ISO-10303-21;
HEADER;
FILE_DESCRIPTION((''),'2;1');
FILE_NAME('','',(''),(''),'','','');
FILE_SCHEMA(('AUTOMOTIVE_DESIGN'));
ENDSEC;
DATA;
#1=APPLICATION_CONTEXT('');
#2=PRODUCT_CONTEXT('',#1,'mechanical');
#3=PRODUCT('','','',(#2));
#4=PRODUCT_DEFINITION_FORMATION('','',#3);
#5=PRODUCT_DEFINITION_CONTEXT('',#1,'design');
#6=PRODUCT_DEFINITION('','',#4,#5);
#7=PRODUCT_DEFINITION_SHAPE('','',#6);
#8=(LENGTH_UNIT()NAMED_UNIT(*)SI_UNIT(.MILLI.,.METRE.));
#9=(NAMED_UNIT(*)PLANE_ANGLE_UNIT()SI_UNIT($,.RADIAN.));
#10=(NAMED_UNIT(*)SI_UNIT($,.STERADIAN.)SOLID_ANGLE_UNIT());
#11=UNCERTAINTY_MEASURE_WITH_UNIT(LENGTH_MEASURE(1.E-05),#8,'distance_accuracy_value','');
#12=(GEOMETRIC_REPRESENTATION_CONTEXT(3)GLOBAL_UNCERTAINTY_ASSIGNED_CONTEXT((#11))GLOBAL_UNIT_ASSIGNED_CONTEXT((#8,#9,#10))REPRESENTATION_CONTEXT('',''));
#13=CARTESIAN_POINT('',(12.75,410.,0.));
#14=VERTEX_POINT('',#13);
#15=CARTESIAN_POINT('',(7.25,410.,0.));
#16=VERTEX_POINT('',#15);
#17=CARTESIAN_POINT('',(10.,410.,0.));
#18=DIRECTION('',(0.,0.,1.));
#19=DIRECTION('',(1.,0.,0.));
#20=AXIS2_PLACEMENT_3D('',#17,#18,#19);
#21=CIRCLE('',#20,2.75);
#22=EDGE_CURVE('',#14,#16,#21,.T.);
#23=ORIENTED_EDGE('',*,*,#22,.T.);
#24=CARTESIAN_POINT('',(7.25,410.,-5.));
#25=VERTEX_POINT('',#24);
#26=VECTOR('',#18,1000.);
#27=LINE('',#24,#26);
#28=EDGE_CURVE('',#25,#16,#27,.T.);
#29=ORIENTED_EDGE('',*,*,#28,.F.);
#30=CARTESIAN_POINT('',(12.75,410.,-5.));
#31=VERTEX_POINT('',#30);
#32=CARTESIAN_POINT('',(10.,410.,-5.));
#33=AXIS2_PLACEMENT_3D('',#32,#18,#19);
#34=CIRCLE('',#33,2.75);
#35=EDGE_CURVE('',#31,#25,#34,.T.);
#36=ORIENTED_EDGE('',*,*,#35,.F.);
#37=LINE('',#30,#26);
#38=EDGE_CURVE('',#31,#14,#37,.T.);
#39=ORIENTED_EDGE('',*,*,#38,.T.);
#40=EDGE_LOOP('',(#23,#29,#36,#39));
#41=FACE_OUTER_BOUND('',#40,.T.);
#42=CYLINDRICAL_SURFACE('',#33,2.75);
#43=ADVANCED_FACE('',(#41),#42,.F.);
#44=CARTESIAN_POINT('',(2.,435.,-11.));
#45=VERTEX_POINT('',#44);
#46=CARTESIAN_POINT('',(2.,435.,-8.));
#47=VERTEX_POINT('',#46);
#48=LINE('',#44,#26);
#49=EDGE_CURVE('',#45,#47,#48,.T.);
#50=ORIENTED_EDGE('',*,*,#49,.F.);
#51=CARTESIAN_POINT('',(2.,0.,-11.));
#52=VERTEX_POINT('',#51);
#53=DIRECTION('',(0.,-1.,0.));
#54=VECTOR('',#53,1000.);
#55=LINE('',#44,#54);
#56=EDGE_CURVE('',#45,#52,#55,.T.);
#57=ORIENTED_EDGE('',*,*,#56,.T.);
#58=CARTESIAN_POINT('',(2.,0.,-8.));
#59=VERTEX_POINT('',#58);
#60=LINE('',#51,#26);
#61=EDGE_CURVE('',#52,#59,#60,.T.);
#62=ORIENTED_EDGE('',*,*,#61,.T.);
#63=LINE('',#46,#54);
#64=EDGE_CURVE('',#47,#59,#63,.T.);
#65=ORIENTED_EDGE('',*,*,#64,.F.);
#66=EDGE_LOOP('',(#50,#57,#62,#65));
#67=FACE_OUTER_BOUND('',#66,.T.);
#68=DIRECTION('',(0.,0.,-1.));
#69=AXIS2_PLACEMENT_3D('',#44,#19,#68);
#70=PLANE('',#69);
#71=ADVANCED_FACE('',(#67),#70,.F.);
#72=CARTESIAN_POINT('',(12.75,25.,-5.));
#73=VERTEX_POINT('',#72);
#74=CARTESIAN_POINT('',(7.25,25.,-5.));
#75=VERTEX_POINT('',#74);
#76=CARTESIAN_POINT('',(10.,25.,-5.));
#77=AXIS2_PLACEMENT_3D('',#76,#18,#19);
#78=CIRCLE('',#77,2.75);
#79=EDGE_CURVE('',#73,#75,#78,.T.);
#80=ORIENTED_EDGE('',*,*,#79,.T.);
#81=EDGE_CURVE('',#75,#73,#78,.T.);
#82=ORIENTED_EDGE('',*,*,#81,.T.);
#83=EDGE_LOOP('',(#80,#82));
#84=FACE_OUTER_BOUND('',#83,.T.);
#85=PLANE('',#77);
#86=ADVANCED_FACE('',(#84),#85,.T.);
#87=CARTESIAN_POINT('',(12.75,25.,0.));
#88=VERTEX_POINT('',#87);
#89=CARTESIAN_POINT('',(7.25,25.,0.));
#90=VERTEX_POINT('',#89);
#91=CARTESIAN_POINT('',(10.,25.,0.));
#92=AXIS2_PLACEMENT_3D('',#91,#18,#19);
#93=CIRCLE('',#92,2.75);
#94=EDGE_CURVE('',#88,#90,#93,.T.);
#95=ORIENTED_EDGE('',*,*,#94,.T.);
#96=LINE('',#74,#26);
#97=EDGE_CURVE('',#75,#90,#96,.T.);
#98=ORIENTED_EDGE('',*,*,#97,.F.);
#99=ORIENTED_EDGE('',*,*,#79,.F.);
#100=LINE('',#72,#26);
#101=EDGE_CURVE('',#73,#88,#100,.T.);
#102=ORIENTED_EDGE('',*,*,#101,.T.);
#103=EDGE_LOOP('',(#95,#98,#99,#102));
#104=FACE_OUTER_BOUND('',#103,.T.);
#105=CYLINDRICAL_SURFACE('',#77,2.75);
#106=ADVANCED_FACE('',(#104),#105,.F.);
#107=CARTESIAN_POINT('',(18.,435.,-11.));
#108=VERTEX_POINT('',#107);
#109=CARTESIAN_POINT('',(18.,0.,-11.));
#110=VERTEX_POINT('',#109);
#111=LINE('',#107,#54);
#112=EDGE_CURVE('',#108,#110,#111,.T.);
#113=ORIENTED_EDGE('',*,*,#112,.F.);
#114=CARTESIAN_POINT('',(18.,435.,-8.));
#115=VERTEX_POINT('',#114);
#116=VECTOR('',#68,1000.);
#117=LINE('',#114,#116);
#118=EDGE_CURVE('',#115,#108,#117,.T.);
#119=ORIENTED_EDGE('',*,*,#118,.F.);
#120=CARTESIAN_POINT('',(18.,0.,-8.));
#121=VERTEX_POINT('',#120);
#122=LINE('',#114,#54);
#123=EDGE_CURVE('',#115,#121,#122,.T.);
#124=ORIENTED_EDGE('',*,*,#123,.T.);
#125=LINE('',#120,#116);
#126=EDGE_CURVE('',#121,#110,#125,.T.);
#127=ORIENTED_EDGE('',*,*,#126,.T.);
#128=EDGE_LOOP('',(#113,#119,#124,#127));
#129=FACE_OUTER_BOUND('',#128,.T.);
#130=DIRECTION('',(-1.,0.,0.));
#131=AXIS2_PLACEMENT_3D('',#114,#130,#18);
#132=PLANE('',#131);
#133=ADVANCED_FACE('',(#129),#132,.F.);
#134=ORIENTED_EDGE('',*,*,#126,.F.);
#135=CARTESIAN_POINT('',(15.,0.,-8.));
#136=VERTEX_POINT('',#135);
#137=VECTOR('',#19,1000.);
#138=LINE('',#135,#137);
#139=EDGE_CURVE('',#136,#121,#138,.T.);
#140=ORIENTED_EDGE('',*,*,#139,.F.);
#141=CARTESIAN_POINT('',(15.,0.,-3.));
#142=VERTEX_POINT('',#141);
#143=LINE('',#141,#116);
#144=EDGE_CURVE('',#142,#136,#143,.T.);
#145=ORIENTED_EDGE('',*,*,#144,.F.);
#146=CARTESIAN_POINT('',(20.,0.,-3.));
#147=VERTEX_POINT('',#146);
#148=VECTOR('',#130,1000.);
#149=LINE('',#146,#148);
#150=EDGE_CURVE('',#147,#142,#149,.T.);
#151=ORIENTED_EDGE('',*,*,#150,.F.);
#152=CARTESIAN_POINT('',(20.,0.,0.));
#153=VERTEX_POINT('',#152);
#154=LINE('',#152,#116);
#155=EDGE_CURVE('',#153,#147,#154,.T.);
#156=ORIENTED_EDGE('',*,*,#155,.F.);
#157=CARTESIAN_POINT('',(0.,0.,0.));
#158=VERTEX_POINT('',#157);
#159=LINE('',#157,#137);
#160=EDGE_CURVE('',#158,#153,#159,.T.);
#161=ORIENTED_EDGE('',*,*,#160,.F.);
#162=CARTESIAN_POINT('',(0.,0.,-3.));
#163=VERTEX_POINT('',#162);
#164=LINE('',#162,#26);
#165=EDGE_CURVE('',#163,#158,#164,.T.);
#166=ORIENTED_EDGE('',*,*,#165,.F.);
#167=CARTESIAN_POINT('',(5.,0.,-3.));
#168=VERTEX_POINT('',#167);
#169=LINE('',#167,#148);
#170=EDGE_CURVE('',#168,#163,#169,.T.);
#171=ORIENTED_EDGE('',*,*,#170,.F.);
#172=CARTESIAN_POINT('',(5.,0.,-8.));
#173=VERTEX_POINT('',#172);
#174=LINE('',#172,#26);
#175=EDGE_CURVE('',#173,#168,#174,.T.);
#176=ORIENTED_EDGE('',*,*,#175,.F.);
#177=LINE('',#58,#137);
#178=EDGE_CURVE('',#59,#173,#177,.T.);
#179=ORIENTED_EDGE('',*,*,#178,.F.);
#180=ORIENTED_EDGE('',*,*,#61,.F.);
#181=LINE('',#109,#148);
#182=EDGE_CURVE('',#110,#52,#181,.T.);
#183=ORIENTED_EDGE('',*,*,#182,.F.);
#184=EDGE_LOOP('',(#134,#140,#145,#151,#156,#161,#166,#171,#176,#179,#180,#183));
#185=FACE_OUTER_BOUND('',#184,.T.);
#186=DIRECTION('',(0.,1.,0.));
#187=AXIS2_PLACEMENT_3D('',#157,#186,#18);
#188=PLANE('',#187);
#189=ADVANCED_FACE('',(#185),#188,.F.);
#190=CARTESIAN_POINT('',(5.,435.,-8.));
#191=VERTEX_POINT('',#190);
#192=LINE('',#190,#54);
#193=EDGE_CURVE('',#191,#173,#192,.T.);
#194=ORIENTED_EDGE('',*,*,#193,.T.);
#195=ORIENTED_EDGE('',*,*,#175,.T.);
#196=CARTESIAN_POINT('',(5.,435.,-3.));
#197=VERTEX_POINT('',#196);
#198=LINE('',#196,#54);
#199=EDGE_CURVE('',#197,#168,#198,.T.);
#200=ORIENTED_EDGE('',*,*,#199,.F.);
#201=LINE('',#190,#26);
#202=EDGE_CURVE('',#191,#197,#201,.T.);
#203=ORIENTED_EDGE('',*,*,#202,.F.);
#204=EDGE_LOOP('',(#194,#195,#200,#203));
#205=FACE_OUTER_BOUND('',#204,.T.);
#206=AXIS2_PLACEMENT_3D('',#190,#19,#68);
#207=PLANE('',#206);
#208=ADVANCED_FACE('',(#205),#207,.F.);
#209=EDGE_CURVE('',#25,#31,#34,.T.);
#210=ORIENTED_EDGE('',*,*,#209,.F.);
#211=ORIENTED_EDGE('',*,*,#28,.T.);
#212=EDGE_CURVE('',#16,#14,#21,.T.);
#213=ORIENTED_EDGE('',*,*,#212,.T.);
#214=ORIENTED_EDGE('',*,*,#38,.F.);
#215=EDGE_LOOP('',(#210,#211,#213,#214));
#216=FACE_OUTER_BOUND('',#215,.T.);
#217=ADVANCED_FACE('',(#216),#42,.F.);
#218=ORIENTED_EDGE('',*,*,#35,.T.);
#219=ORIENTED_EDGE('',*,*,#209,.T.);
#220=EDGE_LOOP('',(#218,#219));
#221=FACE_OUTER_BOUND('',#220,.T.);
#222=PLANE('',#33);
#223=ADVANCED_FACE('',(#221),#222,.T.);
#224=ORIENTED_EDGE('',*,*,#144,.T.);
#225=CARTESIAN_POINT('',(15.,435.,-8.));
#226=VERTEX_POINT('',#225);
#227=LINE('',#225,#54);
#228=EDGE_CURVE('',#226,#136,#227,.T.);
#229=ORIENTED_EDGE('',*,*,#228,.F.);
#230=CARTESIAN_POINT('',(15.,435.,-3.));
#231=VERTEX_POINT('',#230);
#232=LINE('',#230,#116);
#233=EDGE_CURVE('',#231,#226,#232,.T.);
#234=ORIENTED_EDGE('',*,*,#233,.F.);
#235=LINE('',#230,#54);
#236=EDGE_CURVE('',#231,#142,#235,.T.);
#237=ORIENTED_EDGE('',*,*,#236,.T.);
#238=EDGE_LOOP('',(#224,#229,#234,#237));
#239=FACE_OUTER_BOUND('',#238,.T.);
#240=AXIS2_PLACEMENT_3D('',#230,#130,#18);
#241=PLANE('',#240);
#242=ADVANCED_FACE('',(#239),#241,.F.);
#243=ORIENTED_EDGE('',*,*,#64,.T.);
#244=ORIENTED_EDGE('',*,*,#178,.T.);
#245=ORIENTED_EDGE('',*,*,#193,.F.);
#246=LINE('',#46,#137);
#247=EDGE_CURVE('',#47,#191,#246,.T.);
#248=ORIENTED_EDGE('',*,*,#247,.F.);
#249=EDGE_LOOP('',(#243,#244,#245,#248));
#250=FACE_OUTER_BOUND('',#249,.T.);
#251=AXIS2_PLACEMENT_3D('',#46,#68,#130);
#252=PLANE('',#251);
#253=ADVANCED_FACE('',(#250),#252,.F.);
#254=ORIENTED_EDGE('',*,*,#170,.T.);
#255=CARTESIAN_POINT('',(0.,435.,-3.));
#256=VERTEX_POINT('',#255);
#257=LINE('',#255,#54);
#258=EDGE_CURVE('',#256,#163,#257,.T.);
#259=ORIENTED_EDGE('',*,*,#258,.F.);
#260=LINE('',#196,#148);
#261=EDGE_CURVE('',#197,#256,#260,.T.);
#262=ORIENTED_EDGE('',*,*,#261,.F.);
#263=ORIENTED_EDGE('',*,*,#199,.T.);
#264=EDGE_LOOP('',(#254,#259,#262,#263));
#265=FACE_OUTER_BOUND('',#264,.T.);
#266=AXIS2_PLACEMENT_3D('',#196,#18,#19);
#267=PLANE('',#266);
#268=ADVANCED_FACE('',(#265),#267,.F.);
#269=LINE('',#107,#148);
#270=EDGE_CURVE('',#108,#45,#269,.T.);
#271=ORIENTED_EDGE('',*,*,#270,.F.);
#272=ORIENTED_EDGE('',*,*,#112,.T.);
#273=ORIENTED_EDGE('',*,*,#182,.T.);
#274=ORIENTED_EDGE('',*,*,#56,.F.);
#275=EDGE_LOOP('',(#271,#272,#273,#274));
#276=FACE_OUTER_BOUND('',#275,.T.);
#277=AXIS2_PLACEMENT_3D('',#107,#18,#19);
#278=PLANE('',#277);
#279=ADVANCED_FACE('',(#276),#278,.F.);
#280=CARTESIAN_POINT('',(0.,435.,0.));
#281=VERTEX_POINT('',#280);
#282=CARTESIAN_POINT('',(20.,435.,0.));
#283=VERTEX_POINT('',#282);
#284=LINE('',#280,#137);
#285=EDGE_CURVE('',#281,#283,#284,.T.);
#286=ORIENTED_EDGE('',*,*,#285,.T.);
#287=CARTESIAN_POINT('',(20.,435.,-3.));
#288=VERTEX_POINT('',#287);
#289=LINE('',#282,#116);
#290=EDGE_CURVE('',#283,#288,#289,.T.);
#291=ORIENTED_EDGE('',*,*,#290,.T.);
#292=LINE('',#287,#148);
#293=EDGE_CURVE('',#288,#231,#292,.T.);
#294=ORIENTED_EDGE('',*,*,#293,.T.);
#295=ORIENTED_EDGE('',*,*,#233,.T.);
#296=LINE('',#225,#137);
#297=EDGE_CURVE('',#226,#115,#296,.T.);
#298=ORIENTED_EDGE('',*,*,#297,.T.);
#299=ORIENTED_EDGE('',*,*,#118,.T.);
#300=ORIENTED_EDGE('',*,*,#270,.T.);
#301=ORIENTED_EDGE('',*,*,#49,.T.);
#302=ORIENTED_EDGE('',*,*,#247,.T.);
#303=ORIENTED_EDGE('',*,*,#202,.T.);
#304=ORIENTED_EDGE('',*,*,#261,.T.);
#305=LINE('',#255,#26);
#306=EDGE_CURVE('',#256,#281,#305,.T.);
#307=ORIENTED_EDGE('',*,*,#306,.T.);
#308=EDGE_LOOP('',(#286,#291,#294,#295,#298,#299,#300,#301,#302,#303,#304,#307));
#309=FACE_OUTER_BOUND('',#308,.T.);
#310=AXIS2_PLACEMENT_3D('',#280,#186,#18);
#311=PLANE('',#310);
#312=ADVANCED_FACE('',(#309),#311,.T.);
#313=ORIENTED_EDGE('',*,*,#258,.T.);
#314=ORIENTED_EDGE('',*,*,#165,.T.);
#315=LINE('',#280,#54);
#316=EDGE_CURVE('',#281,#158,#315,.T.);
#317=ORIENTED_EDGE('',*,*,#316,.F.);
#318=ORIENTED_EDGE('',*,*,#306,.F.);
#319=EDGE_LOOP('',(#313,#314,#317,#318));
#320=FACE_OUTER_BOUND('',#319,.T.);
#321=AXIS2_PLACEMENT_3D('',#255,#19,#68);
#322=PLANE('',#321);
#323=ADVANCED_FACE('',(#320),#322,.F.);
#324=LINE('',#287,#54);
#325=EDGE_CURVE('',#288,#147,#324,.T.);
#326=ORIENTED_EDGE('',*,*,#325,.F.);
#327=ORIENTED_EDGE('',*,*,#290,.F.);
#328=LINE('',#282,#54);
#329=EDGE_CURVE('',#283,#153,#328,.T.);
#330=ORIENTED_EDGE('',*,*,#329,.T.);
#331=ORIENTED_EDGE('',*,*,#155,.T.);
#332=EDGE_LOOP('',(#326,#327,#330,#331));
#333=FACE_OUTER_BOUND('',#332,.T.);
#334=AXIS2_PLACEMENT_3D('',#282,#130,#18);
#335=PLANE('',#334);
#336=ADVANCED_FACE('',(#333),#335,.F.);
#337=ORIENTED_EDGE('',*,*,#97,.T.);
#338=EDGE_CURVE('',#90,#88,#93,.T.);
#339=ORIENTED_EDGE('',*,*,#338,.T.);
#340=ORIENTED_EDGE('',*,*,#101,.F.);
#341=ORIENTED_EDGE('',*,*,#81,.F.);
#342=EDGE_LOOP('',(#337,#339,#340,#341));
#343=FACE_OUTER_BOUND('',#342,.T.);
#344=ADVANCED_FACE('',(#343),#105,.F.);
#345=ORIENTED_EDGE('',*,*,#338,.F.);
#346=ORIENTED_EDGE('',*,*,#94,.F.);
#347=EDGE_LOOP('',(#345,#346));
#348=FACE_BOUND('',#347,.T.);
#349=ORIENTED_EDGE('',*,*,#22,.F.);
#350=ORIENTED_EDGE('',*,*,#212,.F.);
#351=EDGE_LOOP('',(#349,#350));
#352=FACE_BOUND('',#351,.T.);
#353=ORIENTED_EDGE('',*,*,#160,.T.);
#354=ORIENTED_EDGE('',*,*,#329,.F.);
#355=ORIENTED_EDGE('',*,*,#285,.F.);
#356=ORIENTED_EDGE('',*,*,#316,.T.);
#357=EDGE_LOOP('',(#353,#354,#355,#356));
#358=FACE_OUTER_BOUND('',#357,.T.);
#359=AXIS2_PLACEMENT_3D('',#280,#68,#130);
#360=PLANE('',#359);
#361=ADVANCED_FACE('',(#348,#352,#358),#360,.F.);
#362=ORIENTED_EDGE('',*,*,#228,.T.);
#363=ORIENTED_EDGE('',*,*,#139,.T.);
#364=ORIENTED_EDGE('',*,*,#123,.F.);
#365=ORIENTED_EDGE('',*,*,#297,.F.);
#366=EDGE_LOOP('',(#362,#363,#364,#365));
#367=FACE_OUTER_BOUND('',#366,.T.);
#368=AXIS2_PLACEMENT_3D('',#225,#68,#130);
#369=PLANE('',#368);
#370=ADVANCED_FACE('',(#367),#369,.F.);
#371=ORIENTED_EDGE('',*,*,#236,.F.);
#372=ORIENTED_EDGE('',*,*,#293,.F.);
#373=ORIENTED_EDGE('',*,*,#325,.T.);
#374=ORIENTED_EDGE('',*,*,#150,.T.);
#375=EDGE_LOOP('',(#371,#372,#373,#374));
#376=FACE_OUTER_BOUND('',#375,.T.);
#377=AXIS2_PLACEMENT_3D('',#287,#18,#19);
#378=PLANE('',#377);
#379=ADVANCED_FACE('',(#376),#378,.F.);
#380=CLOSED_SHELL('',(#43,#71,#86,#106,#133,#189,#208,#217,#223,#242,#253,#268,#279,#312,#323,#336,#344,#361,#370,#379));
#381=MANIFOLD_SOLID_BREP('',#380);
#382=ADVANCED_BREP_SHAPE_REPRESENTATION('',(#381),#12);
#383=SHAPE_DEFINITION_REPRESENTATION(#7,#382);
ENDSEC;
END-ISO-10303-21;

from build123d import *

# Parameters (mm, degrees)
BOSS_EXTRUDE1_DEPTH = 435
SKETCH2_R           = 2.75
CUT_EXTRUDE1_DEPTH  = 5


with BuildPart() as part:
    # Sketch1 → Boss-Extrude1 (new body)
    with BuildSketch(Plane(origin=(0, 0, 0), x_dir=(1, 0, 0), z_dir=(0, 1, 0))):
        Polygon((0, 0), (20, 0), (20, 3), (15, 3), (15, 8), (18, 8), (18, 11), (2, 11), (2, 8), (5, 8), (5, 3), (0, 3), align=None)
    extrude(amount=BOSS_EXTRUDE1_DEPTH)

    # Sketch2 → Cut-Extrude1 (cut)
    with BuildSketch(Plane.XY):
        with Locations((10, 410)):
            Circle(SKETCH2_R)
        with Locations((10, 25)):
            Circle(SKETCH2_R)
    extrude(amount=-CUT_EXTRUDE1_DEPTH, mode=Mode.SUBTRACT)


solid = part.part
